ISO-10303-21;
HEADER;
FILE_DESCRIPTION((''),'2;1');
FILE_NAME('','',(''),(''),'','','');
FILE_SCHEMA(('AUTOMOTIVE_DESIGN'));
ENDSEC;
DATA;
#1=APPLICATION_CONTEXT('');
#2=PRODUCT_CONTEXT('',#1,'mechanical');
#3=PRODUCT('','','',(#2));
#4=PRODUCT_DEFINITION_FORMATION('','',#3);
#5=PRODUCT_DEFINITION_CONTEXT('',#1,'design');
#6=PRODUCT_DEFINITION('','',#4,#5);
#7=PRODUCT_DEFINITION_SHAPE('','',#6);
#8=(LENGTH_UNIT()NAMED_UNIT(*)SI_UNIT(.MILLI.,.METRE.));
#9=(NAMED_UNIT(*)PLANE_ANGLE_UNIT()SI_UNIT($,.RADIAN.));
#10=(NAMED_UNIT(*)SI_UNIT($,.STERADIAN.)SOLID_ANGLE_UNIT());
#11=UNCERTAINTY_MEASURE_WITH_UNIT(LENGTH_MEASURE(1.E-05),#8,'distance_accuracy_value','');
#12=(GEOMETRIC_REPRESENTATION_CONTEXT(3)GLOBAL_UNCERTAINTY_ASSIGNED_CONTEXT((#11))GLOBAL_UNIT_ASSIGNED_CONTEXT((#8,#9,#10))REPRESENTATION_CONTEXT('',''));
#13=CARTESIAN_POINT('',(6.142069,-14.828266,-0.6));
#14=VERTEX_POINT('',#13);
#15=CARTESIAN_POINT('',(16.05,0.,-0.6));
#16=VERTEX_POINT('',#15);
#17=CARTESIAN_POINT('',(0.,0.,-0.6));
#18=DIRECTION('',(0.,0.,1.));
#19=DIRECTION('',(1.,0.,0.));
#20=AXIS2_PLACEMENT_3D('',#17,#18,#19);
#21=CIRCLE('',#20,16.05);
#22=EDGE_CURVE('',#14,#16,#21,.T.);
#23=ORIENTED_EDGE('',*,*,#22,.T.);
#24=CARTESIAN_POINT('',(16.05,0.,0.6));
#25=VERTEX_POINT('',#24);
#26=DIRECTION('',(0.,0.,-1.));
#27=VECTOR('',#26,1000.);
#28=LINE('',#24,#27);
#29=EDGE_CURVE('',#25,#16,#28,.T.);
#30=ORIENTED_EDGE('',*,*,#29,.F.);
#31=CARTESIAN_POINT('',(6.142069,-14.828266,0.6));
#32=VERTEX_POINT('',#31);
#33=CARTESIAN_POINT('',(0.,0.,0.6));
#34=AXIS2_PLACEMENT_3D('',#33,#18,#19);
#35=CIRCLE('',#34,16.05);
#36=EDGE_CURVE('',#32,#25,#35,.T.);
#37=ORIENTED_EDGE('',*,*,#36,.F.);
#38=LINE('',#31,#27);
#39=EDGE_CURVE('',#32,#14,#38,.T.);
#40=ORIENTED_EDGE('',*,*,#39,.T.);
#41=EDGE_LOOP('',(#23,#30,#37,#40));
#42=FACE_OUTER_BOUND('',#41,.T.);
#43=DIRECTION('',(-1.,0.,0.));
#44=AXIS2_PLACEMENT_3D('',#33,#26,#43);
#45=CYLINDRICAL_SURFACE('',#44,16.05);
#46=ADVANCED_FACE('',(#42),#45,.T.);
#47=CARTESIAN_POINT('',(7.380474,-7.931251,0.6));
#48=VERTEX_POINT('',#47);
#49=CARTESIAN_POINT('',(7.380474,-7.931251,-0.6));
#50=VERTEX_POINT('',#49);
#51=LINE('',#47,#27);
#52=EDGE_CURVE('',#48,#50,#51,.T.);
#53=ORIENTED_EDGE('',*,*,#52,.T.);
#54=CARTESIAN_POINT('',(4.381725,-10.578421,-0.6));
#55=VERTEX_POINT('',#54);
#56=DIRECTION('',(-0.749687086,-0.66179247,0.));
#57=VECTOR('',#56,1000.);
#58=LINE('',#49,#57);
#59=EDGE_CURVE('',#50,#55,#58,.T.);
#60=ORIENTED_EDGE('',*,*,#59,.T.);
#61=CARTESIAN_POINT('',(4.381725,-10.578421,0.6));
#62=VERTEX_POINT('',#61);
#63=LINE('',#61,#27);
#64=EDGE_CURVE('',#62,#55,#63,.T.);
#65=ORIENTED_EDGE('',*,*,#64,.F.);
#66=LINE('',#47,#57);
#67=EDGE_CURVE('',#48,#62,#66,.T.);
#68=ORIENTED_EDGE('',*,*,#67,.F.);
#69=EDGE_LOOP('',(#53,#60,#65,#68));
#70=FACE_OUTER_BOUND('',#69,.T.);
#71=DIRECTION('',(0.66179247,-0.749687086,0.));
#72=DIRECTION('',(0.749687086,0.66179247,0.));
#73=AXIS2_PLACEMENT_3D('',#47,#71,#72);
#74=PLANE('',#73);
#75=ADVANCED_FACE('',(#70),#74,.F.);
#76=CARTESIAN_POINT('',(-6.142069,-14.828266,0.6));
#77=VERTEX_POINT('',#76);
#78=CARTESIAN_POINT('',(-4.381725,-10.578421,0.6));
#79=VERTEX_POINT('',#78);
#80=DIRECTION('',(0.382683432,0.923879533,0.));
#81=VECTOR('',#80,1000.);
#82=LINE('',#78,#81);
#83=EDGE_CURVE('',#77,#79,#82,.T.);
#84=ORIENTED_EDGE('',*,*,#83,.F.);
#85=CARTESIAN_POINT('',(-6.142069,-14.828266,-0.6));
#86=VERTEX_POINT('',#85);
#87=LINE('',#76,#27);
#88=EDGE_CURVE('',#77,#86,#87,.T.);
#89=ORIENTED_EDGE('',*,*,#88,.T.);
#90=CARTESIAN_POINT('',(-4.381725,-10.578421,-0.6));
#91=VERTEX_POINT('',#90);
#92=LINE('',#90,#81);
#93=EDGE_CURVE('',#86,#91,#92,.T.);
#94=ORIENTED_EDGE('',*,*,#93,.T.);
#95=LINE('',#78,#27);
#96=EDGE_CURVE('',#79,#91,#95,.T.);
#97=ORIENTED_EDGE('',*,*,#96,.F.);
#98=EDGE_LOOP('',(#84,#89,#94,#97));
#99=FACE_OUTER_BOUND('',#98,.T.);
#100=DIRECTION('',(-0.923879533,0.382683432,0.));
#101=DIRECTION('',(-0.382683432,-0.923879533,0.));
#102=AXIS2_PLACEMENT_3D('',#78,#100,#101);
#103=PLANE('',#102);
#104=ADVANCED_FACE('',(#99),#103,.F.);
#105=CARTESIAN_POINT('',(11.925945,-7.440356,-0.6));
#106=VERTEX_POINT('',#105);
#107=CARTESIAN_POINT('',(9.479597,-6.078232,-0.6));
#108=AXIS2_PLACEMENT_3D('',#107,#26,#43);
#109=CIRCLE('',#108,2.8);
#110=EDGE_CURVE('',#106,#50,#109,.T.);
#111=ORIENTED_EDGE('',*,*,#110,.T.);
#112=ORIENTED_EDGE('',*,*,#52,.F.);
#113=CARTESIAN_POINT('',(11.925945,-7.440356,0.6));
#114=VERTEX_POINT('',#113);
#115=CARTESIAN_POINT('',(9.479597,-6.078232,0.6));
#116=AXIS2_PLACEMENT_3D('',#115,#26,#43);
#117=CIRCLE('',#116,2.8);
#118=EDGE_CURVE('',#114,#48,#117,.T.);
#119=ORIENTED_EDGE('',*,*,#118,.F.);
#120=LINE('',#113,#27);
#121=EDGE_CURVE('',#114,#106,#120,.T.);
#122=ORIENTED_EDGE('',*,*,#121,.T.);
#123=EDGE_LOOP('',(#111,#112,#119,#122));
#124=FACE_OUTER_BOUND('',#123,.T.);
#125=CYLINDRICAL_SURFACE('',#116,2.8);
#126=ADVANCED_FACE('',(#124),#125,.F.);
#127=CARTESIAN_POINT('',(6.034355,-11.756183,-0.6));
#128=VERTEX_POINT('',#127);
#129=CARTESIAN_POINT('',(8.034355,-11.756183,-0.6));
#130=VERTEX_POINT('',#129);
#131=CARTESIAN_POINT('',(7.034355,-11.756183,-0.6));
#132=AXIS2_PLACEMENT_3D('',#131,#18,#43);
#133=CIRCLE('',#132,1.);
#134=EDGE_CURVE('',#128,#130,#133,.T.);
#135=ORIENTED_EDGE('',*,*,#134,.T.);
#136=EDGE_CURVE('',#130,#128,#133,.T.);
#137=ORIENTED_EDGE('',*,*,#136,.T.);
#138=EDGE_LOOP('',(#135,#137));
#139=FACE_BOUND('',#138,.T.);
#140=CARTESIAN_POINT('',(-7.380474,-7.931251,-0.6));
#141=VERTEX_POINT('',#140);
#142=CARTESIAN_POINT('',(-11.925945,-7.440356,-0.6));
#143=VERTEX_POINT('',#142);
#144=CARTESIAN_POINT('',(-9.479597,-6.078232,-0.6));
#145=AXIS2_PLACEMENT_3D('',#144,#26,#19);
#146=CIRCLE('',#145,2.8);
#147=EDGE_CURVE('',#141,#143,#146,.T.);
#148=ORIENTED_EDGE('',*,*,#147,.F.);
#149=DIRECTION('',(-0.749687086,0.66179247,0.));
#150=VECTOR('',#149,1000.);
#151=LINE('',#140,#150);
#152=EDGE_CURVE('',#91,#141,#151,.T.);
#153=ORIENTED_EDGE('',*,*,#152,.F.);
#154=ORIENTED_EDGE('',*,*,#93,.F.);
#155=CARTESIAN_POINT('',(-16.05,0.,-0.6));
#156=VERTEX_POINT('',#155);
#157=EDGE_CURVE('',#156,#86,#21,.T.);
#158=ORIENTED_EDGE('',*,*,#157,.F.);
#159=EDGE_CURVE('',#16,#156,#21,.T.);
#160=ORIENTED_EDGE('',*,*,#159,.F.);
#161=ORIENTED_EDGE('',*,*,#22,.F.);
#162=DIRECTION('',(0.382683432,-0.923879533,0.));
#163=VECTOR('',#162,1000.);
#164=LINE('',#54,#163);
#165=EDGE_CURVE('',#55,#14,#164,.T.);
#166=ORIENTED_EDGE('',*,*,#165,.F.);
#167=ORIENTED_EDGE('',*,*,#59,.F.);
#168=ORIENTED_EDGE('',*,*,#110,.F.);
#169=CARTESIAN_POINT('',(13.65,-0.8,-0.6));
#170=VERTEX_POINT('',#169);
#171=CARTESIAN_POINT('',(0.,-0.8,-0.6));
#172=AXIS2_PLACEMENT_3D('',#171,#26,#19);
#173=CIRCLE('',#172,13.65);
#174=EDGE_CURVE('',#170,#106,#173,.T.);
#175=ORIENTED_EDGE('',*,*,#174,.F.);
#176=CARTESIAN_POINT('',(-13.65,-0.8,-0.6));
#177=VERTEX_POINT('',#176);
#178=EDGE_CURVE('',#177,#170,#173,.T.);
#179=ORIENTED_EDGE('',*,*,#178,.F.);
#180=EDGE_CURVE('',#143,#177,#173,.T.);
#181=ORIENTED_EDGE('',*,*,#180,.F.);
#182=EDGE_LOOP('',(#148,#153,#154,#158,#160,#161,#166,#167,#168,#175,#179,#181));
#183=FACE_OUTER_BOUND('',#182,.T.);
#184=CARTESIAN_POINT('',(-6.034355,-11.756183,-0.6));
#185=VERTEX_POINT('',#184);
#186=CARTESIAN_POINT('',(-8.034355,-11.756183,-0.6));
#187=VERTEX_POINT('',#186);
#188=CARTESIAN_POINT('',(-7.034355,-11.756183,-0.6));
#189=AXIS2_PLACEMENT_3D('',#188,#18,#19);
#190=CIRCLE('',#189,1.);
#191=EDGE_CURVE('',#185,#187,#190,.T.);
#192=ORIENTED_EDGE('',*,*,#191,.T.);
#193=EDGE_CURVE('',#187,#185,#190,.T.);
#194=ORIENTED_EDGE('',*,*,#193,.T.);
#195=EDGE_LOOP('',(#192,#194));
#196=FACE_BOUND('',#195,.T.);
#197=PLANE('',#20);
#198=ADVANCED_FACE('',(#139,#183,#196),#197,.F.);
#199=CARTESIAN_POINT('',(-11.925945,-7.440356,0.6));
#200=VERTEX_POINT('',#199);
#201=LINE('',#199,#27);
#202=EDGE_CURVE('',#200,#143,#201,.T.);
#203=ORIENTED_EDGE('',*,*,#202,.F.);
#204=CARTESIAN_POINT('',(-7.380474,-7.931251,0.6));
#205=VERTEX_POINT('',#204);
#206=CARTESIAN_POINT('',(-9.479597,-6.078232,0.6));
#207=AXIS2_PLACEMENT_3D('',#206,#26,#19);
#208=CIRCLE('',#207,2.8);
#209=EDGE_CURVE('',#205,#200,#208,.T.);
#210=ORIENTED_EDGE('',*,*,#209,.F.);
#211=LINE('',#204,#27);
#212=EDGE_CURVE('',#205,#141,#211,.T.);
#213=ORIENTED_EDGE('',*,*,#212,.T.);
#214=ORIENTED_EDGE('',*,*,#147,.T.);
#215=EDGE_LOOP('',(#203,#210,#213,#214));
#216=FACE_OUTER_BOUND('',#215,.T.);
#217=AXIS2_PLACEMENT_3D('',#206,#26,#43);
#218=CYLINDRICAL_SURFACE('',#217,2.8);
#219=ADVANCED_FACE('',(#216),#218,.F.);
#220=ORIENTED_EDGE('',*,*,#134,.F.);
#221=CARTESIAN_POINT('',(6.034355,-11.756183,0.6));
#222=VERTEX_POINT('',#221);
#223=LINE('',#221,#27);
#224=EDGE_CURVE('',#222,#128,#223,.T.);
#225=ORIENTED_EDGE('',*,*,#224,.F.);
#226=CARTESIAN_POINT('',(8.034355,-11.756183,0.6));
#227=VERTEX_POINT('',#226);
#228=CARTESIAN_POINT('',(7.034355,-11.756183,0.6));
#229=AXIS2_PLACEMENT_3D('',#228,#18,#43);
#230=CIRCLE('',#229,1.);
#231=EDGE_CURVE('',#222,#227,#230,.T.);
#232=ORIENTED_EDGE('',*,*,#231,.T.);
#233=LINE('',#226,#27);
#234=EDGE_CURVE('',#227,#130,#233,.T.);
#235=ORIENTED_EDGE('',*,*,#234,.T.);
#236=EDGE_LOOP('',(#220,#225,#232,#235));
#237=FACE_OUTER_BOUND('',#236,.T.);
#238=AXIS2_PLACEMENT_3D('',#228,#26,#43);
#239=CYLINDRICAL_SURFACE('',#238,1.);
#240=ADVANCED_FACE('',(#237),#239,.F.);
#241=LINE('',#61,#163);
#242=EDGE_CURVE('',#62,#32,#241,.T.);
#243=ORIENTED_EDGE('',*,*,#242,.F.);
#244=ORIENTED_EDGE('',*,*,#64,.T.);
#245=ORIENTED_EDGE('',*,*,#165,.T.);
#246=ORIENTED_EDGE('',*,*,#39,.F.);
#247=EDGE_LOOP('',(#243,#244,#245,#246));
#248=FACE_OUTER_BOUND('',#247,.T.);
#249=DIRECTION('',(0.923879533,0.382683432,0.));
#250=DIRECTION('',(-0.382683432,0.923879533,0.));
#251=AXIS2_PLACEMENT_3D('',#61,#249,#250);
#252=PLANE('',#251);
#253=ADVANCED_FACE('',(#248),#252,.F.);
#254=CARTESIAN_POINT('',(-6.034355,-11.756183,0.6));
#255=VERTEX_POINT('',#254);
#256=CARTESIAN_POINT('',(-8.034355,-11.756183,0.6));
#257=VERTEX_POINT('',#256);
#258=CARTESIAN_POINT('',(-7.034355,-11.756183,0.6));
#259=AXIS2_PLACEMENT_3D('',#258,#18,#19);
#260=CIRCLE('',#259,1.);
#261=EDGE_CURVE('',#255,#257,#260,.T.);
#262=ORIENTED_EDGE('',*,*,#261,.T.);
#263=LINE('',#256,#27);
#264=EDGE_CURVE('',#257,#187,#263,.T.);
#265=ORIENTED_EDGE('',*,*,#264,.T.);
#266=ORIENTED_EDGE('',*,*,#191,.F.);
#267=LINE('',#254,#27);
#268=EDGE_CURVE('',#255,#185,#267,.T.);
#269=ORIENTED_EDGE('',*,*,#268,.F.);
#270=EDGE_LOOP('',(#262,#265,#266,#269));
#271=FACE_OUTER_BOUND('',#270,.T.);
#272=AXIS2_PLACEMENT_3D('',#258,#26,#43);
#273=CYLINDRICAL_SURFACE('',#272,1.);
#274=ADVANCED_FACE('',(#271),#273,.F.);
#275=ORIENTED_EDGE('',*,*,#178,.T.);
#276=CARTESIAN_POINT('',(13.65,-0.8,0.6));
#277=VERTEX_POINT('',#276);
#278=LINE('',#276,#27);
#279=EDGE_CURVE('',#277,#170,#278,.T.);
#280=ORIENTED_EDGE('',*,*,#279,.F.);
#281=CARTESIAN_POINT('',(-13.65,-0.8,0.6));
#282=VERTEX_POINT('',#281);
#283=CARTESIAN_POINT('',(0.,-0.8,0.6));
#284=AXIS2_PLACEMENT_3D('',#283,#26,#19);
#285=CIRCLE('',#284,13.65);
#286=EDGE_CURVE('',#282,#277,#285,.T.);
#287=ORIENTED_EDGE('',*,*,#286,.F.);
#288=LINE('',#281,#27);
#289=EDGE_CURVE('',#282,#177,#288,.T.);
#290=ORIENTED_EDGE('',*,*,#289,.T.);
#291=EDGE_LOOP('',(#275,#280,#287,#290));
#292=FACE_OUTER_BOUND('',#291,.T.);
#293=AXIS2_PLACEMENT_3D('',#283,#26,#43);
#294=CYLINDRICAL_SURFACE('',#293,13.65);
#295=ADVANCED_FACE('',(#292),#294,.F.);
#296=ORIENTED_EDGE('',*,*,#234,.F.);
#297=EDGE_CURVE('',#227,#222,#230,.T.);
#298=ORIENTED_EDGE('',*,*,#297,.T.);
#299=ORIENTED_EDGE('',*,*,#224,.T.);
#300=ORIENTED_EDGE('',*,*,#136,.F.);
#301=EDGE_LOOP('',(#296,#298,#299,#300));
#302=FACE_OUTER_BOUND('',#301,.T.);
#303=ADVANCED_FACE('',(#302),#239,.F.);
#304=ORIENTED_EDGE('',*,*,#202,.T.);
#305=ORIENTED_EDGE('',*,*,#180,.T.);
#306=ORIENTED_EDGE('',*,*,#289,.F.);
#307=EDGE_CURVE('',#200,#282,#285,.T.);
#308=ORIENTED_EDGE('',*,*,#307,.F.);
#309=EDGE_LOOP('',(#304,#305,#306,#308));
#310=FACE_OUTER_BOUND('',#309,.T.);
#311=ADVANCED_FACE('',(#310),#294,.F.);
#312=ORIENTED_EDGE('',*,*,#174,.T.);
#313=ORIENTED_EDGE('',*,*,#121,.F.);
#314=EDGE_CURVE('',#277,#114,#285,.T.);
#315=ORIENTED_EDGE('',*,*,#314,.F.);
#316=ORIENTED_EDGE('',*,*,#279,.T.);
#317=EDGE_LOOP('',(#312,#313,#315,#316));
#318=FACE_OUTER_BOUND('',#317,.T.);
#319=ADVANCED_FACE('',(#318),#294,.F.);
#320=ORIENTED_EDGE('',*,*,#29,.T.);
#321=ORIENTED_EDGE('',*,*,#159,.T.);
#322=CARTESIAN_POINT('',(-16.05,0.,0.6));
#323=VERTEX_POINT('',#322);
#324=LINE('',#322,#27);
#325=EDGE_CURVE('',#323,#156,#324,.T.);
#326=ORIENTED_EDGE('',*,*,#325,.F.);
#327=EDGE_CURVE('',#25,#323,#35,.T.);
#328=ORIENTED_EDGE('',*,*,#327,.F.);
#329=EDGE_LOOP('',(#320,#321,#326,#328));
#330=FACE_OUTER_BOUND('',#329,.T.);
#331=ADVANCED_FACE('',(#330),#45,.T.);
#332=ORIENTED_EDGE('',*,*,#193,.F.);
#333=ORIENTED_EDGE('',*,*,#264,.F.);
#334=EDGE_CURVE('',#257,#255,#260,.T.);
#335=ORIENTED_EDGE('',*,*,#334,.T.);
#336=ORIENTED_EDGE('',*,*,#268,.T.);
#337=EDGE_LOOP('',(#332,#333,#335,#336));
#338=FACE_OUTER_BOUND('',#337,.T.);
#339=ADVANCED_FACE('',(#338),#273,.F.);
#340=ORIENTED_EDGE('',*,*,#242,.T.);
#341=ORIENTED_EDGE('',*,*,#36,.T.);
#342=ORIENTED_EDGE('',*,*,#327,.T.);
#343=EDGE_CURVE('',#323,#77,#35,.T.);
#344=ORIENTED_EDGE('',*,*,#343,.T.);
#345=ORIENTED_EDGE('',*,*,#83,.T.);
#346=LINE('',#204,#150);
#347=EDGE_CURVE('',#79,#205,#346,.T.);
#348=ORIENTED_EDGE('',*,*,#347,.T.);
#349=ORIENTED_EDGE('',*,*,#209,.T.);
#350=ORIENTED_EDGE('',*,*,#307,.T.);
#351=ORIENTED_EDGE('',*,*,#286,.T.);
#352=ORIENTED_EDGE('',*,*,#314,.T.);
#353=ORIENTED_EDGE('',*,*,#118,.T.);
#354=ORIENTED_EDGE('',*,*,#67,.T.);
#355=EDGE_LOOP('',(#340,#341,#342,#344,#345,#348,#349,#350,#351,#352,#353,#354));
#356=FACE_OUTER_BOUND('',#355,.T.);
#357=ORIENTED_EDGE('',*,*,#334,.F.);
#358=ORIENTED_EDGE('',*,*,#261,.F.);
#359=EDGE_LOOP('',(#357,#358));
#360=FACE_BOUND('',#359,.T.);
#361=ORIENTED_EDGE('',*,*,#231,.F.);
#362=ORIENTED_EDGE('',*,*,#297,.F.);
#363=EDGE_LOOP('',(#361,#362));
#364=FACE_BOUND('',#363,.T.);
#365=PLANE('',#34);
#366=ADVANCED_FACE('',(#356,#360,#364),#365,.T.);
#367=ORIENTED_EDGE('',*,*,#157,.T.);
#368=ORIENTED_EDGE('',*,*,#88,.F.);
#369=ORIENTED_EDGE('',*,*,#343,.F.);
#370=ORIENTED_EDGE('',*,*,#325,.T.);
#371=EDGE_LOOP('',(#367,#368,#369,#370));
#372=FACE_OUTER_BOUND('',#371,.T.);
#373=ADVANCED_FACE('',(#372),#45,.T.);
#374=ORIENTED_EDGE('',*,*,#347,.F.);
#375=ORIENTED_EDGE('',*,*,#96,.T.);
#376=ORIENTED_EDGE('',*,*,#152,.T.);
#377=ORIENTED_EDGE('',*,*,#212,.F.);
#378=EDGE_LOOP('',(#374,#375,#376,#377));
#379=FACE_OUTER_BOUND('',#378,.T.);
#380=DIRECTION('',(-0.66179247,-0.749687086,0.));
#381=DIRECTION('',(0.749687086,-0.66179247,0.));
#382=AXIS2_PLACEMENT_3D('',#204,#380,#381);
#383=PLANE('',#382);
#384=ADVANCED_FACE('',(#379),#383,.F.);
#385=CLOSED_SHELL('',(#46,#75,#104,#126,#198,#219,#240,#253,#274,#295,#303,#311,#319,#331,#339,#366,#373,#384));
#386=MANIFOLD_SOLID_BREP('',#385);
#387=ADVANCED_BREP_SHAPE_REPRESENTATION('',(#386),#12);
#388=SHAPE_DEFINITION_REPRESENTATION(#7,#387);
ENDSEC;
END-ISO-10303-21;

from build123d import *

# Parameters (mm, degrees)
EXTRUDE_947_DEPTH      = 0.6
EXTRUDE_947_DEPTH_BACK = 0.6
SKETCH_1_R             = 1


with BuildPart() as part:
    # 草图1 → Extrude 947 (new, two sides: drawn at the far end of the back side and taken through both)
    with BuildSketch(Plane.XY.offset(-EXTRUDE_947_DEPTH_BACK)):
        with BuildLine():
            Line((-7.380473645, -7.931250769), (-4.381725301, -10.578420647))
            Line((-4.381725301, -10.578420647), (-6.142069089, -14.828266497))
            ThreePointArc((-6.142069089, -14.828266497), (0, 16.05), (6.142069089, -14.828266497))
            Line((6.142069089, -14.828266497), (4.381725301, -10.578420647))
            Line((4.381725301, -10.578420647), (7.380473645, -7.931250769))
            ThreePointArc((7.380473645, -7.931250769), (9.780239262, -8.8620448), (11.925945225, -7.440356203))
            ThreePointArc((11.925945225, -7.440356203), (0, 12.85), (-11.925945225, -7.440356203))
            ThreePointArc((-11.925945225, -7.440356203), (-9.780239262, -8.8620448), (-7.380473645, -7.931250769))
        make_face()
        with Locations((-7.034355028, -11.756183451)):
            Circle(SKETCH_1_R, mode=Mode.SUBTRACT)
        with Locations(Location((7.034355028, -11.756183451, 0), (0, 0, 180))):
            Circle(SKETCH_1_R, mode=Mode.SUBTRACT)
    extrude(amount=EXTRUDE_947_DEPTH + EXTRUDE_947_DEPTH_BACK)


solid = part.part
